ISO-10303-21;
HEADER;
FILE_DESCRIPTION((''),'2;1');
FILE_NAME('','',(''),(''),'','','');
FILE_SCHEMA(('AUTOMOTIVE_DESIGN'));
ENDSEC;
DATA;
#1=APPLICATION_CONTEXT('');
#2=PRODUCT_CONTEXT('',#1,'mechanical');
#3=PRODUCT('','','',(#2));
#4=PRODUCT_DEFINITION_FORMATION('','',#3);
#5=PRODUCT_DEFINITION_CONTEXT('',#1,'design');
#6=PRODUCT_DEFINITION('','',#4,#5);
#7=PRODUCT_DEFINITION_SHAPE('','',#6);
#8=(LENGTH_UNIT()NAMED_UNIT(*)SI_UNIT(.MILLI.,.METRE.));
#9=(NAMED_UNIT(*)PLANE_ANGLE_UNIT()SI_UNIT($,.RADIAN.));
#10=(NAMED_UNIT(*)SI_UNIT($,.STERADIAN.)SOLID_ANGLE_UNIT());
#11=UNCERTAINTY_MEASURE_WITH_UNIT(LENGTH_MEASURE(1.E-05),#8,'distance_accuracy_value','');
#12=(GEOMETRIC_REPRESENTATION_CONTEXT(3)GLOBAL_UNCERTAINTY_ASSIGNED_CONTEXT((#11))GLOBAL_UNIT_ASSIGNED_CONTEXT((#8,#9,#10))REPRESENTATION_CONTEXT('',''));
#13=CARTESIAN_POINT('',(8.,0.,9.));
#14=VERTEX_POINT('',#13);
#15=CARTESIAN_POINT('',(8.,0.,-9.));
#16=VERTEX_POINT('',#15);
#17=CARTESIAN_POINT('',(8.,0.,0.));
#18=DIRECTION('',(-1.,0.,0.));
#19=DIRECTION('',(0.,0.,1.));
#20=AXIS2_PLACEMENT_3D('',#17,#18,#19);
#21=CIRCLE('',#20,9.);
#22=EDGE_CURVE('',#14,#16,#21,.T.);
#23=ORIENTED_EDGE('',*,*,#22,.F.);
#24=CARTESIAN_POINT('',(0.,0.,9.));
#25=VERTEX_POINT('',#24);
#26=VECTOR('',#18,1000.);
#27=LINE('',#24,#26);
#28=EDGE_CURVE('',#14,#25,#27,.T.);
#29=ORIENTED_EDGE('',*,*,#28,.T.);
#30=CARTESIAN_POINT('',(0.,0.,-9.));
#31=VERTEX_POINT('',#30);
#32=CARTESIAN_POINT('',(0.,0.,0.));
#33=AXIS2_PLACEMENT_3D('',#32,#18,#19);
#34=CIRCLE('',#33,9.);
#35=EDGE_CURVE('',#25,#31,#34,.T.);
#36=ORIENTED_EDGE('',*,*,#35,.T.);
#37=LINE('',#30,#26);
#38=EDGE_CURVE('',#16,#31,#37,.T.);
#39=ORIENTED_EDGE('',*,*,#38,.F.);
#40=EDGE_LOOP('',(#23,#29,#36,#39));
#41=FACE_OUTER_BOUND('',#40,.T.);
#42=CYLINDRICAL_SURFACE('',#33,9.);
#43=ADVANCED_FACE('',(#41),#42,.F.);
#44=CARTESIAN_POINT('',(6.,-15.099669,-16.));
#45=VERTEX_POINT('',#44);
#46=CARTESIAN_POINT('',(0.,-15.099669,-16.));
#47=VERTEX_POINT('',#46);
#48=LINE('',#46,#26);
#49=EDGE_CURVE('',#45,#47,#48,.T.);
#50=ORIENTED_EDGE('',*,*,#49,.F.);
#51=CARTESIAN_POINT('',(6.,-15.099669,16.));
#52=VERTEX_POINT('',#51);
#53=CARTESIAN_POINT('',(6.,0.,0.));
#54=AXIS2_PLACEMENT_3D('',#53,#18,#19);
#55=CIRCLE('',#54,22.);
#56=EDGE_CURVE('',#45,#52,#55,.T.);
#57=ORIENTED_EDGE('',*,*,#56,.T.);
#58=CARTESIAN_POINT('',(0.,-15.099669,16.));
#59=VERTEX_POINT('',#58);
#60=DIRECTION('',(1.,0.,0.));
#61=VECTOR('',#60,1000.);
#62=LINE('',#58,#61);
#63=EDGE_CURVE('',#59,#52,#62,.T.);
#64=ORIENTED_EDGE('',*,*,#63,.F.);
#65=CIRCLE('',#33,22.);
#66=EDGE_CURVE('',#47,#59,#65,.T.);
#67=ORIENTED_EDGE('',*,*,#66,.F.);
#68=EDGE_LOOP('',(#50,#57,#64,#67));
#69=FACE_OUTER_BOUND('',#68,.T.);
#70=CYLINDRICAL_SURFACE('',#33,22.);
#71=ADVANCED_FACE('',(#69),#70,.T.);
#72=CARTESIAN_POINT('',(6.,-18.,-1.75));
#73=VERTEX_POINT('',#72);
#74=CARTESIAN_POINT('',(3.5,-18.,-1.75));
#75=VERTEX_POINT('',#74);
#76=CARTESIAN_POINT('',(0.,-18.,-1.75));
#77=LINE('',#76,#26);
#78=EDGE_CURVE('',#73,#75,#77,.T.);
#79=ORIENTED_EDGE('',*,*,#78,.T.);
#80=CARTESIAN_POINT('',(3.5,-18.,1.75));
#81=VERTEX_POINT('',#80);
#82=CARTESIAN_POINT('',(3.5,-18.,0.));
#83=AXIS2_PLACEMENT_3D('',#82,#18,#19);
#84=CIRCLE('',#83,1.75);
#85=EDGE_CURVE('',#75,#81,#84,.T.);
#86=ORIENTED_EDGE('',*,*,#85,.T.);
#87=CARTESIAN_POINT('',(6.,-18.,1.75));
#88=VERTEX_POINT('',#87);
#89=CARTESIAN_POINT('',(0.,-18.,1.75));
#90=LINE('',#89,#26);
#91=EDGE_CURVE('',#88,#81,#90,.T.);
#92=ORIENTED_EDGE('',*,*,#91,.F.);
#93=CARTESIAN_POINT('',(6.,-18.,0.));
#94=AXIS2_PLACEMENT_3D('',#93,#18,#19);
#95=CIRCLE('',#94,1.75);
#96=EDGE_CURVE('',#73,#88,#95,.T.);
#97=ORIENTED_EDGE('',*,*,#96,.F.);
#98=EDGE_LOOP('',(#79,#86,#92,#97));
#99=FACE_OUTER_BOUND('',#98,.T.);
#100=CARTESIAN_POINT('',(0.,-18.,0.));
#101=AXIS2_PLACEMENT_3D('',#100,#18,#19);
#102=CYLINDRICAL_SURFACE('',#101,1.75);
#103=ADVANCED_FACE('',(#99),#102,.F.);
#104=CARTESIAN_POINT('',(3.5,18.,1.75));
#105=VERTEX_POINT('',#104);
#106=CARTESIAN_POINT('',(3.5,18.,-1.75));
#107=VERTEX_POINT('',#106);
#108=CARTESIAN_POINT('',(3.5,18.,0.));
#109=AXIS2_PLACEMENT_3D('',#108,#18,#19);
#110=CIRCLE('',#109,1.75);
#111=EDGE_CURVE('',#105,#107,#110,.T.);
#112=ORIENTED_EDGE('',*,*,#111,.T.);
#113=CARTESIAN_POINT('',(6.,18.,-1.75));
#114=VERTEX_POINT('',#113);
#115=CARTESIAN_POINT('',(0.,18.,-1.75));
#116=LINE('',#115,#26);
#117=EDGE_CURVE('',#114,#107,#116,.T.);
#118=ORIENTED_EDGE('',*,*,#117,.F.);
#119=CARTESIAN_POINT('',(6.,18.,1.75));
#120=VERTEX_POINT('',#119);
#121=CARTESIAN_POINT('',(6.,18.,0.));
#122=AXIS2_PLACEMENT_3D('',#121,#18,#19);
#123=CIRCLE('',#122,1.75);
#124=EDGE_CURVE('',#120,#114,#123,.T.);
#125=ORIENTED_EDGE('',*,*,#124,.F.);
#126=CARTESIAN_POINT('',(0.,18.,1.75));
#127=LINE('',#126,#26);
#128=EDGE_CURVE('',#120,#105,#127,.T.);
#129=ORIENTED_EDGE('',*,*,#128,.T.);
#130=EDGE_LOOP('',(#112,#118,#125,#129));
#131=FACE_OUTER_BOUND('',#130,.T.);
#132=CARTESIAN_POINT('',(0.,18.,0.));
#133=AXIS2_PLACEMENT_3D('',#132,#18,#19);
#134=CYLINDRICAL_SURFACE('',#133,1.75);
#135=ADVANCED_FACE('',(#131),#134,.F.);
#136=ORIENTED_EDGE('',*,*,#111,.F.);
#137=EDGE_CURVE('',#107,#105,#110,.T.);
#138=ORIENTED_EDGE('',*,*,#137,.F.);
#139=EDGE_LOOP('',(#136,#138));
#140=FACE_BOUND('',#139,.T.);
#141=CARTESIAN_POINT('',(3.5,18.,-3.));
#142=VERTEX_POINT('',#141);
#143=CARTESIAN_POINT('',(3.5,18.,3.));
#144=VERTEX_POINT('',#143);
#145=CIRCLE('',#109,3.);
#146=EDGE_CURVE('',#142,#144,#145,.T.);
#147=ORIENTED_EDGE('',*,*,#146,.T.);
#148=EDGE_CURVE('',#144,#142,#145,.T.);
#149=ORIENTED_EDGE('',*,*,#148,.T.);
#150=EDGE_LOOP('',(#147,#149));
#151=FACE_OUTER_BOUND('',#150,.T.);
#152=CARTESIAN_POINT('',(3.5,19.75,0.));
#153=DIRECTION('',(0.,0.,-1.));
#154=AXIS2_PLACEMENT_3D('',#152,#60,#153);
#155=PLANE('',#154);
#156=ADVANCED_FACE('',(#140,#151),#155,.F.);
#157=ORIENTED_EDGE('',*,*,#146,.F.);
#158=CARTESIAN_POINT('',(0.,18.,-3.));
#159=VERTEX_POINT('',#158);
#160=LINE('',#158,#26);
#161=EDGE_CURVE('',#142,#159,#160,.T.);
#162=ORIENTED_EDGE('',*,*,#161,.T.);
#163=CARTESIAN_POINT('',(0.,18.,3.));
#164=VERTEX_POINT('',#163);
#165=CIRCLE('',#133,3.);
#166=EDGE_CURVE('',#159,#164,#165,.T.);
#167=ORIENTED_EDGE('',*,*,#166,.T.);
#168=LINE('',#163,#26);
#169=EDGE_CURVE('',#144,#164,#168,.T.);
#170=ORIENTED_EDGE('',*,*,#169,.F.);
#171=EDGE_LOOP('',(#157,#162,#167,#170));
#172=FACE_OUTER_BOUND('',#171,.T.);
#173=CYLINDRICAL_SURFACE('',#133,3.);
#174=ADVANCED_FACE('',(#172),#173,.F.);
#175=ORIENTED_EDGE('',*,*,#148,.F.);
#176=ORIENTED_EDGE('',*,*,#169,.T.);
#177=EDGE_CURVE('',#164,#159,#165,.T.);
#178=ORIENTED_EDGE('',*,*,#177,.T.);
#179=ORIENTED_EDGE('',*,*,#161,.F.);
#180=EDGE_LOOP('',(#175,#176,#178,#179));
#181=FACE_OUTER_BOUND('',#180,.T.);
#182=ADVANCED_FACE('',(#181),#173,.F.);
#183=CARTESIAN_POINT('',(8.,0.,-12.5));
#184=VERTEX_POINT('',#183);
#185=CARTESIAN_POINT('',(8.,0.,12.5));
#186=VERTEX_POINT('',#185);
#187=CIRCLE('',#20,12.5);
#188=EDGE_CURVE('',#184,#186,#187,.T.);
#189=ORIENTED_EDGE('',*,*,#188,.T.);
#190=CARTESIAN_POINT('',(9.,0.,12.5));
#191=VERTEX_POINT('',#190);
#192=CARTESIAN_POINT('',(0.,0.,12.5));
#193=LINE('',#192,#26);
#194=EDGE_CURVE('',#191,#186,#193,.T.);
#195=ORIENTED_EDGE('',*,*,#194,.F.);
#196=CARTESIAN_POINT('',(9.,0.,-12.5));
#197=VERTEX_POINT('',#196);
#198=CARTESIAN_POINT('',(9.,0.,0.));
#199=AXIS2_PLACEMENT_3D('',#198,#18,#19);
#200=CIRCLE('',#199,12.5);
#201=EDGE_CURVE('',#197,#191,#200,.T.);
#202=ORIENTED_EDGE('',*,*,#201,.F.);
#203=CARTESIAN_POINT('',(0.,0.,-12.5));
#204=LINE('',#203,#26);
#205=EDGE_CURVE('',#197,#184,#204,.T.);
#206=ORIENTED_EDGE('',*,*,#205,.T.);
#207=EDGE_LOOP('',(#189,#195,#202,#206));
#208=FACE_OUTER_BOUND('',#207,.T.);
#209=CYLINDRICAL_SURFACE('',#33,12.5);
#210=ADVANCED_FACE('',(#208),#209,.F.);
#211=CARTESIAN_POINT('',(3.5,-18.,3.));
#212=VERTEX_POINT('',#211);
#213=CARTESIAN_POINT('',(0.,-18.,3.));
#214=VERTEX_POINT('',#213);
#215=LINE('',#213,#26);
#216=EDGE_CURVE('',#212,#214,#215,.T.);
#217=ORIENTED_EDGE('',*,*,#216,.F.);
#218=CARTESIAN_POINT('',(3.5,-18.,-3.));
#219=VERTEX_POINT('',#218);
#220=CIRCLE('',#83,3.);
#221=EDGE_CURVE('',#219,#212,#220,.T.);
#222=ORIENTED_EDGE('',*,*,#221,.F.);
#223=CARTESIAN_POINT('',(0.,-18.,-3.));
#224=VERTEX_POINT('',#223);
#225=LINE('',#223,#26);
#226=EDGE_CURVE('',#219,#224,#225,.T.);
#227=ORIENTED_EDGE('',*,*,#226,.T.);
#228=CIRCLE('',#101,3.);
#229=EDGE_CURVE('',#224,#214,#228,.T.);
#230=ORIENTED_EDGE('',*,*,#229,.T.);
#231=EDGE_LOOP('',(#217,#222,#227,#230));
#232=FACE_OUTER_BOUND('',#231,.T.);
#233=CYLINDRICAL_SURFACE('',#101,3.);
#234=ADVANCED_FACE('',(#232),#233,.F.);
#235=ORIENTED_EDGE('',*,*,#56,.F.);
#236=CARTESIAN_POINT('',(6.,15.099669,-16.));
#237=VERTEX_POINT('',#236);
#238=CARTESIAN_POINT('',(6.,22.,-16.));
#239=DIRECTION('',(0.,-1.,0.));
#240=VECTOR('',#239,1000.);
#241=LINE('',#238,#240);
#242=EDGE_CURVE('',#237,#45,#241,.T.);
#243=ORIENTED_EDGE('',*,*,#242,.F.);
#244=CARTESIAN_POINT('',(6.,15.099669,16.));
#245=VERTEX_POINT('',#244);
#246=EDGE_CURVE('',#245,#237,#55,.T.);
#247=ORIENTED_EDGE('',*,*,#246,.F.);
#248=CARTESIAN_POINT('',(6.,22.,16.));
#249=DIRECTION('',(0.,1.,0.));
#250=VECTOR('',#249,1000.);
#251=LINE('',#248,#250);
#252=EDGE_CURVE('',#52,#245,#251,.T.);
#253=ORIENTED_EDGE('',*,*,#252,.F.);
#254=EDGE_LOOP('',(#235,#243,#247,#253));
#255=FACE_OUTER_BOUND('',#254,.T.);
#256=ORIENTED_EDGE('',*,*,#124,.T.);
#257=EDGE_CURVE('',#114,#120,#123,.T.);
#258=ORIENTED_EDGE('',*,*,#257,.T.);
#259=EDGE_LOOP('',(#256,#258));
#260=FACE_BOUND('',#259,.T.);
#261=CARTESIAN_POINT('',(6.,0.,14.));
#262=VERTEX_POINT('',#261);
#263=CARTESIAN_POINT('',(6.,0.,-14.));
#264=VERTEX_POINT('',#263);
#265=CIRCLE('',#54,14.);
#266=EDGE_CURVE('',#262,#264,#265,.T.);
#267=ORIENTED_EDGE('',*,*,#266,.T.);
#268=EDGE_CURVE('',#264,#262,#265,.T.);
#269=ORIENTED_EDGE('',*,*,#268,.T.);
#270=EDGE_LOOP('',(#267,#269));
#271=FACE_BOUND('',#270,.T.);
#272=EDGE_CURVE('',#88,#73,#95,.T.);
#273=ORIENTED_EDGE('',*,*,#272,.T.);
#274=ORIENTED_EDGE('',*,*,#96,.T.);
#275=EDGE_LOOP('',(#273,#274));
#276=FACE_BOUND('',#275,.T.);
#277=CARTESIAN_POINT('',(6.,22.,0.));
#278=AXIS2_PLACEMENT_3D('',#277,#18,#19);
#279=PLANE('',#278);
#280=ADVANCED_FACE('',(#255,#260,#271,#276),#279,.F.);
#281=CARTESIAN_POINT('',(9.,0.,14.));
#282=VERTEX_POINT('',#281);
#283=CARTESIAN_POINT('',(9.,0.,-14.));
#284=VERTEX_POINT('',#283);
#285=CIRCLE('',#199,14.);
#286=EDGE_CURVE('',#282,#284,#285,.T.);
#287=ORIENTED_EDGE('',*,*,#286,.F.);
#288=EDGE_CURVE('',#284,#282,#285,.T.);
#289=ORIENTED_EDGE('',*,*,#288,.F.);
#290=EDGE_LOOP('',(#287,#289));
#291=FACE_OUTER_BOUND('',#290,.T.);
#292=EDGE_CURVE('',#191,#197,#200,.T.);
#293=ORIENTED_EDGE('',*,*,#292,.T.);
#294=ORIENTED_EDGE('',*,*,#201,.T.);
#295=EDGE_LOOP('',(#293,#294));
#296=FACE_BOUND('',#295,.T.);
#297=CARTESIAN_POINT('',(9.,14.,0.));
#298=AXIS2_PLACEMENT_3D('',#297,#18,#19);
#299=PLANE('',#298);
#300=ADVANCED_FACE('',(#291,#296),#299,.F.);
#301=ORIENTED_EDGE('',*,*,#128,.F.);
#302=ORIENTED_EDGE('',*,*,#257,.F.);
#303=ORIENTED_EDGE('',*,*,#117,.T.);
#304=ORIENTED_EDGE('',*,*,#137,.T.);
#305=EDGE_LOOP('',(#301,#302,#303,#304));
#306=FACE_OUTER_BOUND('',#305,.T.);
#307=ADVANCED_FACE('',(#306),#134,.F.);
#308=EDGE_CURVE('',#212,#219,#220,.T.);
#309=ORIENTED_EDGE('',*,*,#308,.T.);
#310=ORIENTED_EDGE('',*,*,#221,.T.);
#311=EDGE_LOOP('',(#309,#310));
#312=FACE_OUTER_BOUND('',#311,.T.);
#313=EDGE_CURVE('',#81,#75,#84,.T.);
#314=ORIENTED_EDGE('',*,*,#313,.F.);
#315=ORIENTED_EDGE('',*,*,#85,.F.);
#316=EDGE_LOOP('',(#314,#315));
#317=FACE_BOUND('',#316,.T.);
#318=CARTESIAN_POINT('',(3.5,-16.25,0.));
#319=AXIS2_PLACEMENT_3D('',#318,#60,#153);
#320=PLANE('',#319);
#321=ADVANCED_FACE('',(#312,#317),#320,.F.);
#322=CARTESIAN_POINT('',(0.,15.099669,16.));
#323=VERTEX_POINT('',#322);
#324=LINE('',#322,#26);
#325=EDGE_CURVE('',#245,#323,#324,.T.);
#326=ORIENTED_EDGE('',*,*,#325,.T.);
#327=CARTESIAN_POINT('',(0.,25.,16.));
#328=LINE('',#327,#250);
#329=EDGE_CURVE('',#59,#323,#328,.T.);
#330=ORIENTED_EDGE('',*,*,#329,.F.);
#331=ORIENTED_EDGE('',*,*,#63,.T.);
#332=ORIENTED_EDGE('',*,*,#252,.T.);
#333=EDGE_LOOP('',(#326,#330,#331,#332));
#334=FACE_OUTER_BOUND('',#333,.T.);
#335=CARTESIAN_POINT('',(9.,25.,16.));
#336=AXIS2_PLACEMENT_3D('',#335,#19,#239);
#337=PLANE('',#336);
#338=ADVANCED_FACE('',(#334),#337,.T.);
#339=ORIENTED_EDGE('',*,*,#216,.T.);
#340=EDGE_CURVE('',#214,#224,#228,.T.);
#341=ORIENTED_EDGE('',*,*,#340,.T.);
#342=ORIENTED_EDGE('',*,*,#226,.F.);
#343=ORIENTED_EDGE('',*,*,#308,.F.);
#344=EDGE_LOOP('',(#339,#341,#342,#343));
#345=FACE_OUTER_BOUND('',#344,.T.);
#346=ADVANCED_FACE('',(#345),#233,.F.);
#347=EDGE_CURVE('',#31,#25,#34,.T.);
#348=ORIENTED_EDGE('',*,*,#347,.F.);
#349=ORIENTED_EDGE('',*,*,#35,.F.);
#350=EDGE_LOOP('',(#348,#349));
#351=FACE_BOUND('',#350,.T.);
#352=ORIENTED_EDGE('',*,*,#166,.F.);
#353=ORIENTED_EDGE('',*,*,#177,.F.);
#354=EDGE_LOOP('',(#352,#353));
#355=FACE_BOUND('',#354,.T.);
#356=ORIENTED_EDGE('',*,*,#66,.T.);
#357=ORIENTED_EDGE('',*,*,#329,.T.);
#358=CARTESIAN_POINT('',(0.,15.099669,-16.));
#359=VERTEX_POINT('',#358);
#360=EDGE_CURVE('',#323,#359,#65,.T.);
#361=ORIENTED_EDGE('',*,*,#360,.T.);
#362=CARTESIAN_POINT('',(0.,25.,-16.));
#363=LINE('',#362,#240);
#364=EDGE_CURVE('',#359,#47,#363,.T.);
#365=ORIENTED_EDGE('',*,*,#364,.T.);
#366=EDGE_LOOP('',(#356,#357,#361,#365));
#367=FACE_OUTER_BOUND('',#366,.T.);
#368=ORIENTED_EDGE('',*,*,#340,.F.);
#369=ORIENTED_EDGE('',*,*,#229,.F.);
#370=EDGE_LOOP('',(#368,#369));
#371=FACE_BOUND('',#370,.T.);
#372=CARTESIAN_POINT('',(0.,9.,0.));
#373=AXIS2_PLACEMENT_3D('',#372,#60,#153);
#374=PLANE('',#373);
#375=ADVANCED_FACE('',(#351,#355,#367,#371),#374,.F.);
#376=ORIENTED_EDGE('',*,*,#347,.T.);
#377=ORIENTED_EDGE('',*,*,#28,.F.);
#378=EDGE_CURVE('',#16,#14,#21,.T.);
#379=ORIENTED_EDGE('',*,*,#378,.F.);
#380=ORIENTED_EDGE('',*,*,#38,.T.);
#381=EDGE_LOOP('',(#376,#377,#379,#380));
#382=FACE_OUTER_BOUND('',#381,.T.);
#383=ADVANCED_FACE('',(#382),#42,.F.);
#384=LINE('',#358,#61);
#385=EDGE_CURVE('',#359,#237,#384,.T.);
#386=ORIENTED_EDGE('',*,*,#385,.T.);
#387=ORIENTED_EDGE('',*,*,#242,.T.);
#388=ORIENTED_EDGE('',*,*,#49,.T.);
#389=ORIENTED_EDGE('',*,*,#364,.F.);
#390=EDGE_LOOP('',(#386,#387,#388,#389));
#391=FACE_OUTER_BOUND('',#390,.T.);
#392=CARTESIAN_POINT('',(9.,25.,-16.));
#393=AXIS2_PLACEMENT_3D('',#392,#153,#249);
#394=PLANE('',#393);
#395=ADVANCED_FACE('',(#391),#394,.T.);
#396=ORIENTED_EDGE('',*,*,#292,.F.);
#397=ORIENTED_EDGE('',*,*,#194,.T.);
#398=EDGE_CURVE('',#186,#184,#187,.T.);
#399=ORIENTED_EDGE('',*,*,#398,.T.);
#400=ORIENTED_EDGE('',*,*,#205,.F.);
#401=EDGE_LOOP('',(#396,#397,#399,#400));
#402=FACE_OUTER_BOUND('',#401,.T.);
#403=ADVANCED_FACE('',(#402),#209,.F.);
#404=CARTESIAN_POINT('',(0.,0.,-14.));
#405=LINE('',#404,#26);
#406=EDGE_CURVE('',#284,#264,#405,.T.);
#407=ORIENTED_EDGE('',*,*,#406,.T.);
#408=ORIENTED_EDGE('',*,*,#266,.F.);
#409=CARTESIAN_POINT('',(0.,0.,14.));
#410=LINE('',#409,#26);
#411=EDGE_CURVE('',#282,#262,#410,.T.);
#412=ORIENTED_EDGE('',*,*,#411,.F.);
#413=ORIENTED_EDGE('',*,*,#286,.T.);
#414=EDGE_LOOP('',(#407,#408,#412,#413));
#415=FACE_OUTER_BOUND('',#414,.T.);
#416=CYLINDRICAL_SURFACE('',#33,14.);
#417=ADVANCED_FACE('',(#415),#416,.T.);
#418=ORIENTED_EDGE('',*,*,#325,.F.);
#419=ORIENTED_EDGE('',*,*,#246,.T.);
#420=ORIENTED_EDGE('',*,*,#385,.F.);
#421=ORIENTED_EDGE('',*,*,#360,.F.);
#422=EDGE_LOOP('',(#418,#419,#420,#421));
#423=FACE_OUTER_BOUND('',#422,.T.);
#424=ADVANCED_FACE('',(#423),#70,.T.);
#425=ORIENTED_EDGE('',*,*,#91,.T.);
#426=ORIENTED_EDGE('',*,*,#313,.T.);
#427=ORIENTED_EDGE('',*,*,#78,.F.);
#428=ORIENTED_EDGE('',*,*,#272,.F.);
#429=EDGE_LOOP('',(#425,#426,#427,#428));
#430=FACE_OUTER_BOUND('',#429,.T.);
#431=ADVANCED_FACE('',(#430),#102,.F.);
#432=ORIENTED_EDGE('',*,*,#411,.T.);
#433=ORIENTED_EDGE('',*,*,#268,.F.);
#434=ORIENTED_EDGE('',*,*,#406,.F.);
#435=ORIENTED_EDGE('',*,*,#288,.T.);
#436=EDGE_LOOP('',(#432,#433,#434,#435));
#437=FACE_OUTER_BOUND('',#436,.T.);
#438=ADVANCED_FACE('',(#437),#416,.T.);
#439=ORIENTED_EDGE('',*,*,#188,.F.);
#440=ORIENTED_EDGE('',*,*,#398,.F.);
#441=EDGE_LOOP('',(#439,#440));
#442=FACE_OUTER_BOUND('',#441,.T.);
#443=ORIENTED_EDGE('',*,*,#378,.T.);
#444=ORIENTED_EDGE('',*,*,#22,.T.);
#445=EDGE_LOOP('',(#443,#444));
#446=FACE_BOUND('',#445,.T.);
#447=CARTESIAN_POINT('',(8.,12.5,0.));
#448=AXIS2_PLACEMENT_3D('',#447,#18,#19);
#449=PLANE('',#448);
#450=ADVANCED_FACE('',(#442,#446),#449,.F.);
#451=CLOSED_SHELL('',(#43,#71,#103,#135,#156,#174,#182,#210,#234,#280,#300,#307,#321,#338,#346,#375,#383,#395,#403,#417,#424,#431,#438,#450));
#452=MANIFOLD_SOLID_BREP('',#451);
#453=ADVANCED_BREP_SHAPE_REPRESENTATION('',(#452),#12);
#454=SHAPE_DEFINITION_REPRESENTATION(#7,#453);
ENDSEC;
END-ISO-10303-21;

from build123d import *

# Parameters (mm, degrees)
SKETCH3_OUTSIDE_W                       = 58.574
SKETCH3_OUTSIDE_H                       = 58.574
SKETCH3_OUTSIDE_W_2                     = 32
SKETCH3_OUTSIDE_H_2                     = 50
CUT_EXTRUDE1_DEPTH                      = 33.388269481
CBORE_FOR_M3_HEX_HEAD_BOLT1_D           = 3.5
CBORE_FOR_M3_HEX_HEAD_BOLT1_CBORE_D     = 6
CBORE_FOR_M3_HEX_HEAD_BOLT1_CBORE_DEPTH = 3.5


with BuildPart() as part:
    # Sketch1 → Revolve1 (revolve)
    with BuildSketch(Plane.XY, mode=Mode.PRIVATE) as revolve1_sk:
        Polygon((0, 9), (0, 22), (6, 22), (6, 14), (9, 14), (9, 12.5), (8, 12.5), (8, 9), align=None)
    revolve(revolve1_sk.sketch.rotate(Axis((0, 0, 0), (1, 0, 0)), 90), axis=Axis((0, 0, 0), (1, 0, 0)))

    # Sketch3 outside → Cut-Extrude1 (cut, through all)
    with BuildSketch(Plane.ZY):
        Rectangle(SKETCH3_OUTSIDE_W, SKETCH3_OUTSIDE_H)
        Rectangle(SKETCH3_OUTSIDE_W_2, SKETCH3_OUTSIDE_H_2, mode=Mode.SUBTRACT)
    extrude(amount=-CUT_EXTRUDE1_DEPTH, mode=Mode.SUBTRACT)

    # CBORE for M3 Hex Head Bolt1 (through all)
    with Locations(Plane.ZY):
        with Locations((0, 18), (0, -18)):
            CounterBoreHole(CBORE_FOR_M3_HEX_HEAD_BOLT1_D / 2, CBORE_FOR_M3_HEX_HEAD_BOLT1_CBORE_D / 2, CBORE_FOR_M3_HEX_HEAD_BOLT1_CBORE_DEPTH)


solid = part.part
